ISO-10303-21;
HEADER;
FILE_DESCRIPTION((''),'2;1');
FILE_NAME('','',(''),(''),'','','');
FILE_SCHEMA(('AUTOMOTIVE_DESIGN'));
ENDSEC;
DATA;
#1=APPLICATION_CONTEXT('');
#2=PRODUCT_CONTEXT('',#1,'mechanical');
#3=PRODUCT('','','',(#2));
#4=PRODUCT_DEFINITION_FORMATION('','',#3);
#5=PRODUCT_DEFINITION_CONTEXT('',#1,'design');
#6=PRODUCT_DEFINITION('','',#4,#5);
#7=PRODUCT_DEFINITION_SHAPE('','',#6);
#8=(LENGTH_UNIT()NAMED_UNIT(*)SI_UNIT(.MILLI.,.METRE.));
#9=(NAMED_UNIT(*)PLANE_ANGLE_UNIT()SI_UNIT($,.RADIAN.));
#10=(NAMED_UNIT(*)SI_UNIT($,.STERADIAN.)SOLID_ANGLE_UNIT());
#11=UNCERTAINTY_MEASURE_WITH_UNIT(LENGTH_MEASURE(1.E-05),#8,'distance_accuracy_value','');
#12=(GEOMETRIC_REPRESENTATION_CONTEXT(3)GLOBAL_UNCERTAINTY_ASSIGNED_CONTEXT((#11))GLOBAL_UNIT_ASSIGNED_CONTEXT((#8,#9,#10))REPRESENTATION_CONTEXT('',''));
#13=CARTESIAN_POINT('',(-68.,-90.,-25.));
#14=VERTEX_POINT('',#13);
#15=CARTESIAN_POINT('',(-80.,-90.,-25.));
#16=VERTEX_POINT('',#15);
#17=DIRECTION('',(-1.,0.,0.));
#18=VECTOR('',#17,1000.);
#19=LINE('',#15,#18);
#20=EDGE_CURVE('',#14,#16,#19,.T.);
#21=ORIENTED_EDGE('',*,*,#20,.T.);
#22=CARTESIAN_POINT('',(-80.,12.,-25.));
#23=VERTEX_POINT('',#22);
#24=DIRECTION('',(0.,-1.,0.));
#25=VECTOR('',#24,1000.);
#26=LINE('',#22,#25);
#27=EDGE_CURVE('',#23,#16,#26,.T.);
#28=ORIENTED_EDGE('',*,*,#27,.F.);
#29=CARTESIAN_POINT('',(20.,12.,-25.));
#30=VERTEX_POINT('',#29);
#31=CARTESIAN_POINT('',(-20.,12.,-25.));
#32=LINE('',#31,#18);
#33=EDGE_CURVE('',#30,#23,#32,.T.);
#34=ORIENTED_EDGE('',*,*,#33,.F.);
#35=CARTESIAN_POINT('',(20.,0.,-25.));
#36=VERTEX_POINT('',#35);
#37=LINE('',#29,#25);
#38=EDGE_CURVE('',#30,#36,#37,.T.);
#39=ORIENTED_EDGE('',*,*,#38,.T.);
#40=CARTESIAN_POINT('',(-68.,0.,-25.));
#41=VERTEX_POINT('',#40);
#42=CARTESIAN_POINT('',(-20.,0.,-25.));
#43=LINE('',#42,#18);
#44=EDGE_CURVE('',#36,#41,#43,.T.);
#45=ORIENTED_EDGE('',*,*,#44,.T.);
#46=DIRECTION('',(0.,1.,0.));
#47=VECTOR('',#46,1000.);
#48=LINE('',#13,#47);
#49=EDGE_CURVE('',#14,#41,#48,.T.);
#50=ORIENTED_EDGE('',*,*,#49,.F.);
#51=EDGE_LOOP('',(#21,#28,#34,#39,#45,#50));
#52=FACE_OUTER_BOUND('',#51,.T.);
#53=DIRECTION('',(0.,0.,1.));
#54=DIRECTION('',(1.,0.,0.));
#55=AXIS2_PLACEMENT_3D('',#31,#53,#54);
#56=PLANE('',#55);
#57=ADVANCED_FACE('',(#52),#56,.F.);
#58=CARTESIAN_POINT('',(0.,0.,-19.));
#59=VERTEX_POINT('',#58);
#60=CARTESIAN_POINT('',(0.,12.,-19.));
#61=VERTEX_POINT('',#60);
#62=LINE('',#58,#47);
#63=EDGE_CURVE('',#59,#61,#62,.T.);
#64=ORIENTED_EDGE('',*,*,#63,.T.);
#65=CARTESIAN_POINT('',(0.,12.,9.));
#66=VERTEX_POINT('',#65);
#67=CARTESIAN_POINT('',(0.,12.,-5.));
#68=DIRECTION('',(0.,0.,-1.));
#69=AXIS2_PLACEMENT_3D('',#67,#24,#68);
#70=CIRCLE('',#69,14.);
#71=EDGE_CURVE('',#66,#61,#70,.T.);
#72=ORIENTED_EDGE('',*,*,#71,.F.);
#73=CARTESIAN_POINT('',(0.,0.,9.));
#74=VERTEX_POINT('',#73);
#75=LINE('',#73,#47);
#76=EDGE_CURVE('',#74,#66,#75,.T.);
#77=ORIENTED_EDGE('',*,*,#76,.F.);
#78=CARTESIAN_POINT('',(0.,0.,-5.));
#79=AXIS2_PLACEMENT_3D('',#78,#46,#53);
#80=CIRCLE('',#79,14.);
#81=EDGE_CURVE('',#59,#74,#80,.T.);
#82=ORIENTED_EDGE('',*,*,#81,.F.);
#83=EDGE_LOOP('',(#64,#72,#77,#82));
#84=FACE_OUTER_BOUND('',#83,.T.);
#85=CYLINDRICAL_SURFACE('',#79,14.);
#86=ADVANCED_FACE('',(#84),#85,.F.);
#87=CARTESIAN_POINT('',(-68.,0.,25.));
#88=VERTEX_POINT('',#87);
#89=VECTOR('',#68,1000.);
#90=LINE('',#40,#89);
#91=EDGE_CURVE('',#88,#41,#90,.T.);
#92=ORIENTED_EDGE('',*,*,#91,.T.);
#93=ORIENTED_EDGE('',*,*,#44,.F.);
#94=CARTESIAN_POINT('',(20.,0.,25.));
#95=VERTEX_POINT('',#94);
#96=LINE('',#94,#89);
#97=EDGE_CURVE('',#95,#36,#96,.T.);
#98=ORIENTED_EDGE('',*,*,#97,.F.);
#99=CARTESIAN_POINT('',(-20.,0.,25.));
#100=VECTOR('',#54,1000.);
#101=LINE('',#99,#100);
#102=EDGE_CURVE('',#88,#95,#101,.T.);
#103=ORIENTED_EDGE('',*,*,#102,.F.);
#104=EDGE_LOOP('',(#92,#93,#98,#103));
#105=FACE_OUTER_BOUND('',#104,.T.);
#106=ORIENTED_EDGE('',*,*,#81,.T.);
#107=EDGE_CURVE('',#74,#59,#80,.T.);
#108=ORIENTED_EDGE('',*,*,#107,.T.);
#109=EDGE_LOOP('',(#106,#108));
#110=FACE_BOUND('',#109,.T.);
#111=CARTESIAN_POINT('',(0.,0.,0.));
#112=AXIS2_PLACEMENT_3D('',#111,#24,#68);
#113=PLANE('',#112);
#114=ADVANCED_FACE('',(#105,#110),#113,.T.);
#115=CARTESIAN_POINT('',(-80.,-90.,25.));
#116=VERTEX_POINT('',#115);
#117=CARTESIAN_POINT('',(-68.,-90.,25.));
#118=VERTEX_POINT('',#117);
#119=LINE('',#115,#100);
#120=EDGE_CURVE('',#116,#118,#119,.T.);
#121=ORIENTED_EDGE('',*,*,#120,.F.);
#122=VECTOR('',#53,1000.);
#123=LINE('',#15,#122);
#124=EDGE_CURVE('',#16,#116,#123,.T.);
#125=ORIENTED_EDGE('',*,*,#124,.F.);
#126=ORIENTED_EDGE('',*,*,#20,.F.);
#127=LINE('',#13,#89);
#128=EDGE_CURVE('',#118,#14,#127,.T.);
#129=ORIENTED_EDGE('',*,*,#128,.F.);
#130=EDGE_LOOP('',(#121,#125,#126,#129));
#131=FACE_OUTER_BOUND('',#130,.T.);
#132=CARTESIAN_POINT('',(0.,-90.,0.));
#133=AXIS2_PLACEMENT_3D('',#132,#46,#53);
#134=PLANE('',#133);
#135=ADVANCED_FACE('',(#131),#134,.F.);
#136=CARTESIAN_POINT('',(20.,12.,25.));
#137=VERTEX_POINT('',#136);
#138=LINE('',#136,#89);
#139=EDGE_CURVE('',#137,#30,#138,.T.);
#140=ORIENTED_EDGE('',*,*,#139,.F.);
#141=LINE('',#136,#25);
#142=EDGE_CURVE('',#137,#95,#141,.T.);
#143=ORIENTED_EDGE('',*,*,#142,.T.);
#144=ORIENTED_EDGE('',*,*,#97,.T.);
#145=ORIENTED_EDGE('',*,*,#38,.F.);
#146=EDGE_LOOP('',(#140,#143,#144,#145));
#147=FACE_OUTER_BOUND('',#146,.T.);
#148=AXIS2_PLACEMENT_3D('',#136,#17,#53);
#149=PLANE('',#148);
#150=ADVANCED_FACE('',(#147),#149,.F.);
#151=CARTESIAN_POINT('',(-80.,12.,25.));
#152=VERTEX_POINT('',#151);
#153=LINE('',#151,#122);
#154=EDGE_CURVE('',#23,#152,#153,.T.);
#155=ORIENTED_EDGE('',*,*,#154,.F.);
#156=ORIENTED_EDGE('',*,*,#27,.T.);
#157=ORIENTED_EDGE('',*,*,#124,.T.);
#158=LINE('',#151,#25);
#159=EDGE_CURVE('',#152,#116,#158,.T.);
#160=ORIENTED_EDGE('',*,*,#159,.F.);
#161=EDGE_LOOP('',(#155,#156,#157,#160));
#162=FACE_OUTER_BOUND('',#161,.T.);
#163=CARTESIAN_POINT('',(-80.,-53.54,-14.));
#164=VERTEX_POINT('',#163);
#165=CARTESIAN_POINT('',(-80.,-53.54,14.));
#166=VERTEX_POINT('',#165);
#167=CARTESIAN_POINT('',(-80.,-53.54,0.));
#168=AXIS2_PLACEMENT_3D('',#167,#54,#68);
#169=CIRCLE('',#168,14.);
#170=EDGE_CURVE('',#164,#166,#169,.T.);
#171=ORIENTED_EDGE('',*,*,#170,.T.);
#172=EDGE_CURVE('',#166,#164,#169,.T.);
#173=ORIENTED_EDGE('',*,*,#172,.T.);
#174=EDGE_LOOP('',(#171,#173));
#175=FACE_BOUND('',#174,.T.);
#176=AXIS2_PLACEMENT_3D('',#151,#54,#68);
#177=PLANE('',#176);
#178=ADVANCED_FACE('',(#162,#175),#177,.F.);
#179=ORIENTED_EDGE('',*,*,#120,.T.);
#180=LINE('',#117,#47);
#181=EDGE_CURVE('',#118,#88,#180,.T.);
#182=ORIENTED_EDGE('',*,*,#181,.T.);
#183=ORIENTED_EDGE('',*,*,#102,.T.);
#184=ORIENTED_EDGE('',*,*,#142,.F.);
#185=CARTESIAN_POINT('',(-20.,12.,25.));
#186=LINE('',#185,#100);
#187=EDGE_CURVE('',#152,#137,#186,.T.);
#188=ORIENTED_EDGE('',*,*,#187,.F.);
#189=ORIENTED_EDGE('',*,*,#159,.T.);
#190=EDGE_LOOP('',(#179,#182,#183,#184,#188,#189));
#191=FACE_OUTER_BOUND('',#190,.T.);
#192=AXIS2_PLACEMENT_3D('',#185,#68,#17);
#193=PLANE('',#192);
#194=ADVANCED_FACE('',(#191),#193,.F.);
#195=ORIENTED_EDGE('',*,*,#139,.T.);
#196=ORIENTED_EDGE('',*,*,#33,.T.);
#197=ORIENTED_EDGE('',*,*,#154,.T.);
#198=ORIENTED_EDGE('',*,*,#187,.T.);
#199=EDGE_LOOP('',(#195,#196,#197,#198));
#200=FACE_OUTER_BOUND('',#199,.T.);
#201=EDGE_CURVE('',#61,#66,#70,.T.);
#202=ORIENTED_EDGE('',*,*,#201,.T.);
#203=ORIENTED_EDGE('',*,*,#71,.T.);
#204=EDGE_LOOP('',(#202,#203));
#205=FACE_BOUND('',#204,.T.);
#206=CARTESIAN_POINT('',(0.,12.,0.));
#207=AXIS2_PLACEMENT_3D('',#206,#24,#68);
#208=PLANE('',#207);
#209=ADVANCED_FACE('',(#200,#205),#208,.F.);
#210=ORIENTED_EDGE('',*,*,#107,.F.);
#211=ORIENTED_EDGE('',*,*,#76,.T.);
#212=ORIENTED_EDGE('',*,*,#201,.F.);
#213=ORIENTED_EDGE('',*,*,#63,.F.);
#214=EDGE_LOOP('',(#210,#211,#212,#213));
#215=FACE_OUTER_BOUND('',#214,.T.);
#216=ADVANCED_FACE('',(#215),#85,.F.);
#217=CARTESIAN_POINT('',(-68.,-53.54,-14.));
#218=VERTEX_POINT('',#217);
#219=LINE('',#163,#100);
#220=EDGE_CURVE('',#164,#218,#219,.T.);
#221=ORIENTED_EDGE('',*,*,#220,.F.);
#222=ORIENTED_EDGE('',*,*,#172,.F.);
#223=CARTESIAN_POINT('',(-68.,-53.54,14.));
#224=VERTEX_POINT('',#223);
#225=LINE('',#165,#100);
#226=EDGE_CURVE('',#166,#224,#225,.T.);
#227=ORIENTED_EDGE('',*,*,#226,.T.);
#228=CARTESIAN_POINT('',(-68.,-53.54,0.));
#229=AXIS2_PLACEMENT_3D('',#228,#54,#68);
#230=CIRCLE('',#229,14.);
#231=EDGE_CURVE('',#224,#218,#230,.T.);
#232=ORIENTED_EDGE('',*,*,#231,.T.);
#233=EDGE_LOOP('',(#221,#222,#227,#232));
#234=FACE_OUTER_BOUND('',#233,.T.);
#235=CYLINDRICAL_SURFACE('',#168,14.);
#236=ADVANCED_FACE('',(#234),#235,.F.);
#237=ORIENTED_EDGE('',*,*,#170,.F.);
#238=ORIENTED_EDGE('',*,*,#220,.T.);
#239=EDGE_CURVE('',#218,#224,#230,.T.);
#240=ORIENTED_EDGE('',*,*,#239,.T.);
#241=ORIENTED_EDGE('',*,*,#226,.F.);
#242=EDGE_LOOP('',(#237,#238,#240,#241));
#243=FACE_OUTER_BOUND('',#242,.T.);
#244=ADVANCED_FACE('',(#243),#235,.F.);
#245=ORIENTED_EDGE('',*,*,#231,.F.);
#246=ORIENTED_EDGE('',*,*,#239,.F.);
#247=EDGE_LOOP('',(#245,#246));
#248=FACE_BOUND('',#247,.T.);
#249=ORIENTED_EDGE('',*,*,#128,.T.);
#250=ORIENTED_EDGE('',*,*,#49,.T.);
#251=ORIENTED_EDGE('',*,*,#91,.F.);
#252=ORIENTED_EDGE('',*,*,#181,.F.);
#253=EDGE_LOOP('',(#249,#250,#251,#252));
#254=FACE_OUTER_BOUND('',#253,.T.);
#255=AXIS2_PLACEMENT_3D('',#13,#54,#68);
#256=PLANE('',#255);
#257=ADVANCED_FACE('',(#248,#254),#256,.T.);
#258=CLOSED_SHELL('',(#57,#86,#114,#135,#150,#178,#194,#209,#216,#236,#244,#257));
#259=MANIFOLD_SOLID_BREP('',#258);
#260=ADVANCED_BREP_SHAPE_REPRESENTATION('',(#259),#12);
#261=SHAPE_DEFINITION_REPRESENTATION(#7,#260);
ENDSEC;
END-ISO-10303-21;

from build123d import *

# Parameters (mm, degrees)
SKETCH1_W               = 40
SKETCH1_H               = 50
BOSS_EXTRUDE1_DEPTH     = 12
CUT_EXTRUDE1_DEPTH      = 35.190641995
CUT_EXTRUDE1_DEPTH_BACK = 35.190641995
SKETCH2_R               = 14
MOVE_FACE2_BY           = 60
SKETCH3_W               = 12
SKETCH3_H               = 50
BOSS_EXTRUDE2_DEPTH     = 90
CUT_EXTRUDE2_DEPTH      = 129.33160172
CUT_EXTRUDE2_DEPTH_BACK = 129.33160172
SKETCH4_R               = 14


with BuildPart() as part:
    # Sketch1 → Boss-Extrude1 (new body)
    with BuildSketch(Plane(origin=(0, 0, 0), x_dir=(1, 0, 0), z_dir=(0, 1, 0))):
        Rectangle(SKETCH1_W, SKETCH1_H)
    extrude(amount=BOSS_EXTRUDE1_DEPTH)

    # Sketch2 → Cut-Extrude1 (cut, two sides: drawn at the far end of the back side and taken through both)
    with BuildSketch(Plane(origin=(0, 12, 0), x_dir=(1, 0, 0), z_dir=(0, 1, 0)).offset(-CUT_EXTRUDE1_DEPTH_BACK)):
        with Locations(Location((0, 5, 0), (0, 0, 270))):
            Circle(SKETCH2_R)
    extrude(amount=CUT_EXTRUDE1_DEPTH + CUT_EXTRUDE1_DEPTH_BACK, mode=Mode.SUBTRACT)

    # Move Face2: a face moved outward by 60.0
    extrude(part.faces().sort_by_distance((-20, 6, 0))[0], amount=MOVE_FACE2_BY, dir=(-1, 0, 0))

    # Sketch3 → Boss-Extrude2 (add)
    with BuildSketch(Plane(origin=(0, 0, 0), x_dir=(1, 0, 0), z_dir=(0, 1, 0))):
        with Locations((-74, 0)):
            Rectangle(SKETCH3_W, SKETCH3_H)
    extrude(amount=-BOSS_EXTRUDE2_DEPTH)

    # Sketch4 → Cut-Extrude2 (cut, two sides: drawn at the far end of the back side and taken through both)
    with BuildSketch(Plane(origin=(-68, 0, 0), x_dir=(0, 0, -1), z_dir=(1, 0, 0)).offset(-CUT_EXTRUDE2_DEPTH_BACK)):
        with Locations((0, -53.54)):
            Circle(SKETCH4_R)
    extrude(amount=CUT_EXTRUDE2_DEPTH + CUT_EXTRUDE2_DEPTH_BACK, mode=Mode.SUBTRACT)


solid = part.part
